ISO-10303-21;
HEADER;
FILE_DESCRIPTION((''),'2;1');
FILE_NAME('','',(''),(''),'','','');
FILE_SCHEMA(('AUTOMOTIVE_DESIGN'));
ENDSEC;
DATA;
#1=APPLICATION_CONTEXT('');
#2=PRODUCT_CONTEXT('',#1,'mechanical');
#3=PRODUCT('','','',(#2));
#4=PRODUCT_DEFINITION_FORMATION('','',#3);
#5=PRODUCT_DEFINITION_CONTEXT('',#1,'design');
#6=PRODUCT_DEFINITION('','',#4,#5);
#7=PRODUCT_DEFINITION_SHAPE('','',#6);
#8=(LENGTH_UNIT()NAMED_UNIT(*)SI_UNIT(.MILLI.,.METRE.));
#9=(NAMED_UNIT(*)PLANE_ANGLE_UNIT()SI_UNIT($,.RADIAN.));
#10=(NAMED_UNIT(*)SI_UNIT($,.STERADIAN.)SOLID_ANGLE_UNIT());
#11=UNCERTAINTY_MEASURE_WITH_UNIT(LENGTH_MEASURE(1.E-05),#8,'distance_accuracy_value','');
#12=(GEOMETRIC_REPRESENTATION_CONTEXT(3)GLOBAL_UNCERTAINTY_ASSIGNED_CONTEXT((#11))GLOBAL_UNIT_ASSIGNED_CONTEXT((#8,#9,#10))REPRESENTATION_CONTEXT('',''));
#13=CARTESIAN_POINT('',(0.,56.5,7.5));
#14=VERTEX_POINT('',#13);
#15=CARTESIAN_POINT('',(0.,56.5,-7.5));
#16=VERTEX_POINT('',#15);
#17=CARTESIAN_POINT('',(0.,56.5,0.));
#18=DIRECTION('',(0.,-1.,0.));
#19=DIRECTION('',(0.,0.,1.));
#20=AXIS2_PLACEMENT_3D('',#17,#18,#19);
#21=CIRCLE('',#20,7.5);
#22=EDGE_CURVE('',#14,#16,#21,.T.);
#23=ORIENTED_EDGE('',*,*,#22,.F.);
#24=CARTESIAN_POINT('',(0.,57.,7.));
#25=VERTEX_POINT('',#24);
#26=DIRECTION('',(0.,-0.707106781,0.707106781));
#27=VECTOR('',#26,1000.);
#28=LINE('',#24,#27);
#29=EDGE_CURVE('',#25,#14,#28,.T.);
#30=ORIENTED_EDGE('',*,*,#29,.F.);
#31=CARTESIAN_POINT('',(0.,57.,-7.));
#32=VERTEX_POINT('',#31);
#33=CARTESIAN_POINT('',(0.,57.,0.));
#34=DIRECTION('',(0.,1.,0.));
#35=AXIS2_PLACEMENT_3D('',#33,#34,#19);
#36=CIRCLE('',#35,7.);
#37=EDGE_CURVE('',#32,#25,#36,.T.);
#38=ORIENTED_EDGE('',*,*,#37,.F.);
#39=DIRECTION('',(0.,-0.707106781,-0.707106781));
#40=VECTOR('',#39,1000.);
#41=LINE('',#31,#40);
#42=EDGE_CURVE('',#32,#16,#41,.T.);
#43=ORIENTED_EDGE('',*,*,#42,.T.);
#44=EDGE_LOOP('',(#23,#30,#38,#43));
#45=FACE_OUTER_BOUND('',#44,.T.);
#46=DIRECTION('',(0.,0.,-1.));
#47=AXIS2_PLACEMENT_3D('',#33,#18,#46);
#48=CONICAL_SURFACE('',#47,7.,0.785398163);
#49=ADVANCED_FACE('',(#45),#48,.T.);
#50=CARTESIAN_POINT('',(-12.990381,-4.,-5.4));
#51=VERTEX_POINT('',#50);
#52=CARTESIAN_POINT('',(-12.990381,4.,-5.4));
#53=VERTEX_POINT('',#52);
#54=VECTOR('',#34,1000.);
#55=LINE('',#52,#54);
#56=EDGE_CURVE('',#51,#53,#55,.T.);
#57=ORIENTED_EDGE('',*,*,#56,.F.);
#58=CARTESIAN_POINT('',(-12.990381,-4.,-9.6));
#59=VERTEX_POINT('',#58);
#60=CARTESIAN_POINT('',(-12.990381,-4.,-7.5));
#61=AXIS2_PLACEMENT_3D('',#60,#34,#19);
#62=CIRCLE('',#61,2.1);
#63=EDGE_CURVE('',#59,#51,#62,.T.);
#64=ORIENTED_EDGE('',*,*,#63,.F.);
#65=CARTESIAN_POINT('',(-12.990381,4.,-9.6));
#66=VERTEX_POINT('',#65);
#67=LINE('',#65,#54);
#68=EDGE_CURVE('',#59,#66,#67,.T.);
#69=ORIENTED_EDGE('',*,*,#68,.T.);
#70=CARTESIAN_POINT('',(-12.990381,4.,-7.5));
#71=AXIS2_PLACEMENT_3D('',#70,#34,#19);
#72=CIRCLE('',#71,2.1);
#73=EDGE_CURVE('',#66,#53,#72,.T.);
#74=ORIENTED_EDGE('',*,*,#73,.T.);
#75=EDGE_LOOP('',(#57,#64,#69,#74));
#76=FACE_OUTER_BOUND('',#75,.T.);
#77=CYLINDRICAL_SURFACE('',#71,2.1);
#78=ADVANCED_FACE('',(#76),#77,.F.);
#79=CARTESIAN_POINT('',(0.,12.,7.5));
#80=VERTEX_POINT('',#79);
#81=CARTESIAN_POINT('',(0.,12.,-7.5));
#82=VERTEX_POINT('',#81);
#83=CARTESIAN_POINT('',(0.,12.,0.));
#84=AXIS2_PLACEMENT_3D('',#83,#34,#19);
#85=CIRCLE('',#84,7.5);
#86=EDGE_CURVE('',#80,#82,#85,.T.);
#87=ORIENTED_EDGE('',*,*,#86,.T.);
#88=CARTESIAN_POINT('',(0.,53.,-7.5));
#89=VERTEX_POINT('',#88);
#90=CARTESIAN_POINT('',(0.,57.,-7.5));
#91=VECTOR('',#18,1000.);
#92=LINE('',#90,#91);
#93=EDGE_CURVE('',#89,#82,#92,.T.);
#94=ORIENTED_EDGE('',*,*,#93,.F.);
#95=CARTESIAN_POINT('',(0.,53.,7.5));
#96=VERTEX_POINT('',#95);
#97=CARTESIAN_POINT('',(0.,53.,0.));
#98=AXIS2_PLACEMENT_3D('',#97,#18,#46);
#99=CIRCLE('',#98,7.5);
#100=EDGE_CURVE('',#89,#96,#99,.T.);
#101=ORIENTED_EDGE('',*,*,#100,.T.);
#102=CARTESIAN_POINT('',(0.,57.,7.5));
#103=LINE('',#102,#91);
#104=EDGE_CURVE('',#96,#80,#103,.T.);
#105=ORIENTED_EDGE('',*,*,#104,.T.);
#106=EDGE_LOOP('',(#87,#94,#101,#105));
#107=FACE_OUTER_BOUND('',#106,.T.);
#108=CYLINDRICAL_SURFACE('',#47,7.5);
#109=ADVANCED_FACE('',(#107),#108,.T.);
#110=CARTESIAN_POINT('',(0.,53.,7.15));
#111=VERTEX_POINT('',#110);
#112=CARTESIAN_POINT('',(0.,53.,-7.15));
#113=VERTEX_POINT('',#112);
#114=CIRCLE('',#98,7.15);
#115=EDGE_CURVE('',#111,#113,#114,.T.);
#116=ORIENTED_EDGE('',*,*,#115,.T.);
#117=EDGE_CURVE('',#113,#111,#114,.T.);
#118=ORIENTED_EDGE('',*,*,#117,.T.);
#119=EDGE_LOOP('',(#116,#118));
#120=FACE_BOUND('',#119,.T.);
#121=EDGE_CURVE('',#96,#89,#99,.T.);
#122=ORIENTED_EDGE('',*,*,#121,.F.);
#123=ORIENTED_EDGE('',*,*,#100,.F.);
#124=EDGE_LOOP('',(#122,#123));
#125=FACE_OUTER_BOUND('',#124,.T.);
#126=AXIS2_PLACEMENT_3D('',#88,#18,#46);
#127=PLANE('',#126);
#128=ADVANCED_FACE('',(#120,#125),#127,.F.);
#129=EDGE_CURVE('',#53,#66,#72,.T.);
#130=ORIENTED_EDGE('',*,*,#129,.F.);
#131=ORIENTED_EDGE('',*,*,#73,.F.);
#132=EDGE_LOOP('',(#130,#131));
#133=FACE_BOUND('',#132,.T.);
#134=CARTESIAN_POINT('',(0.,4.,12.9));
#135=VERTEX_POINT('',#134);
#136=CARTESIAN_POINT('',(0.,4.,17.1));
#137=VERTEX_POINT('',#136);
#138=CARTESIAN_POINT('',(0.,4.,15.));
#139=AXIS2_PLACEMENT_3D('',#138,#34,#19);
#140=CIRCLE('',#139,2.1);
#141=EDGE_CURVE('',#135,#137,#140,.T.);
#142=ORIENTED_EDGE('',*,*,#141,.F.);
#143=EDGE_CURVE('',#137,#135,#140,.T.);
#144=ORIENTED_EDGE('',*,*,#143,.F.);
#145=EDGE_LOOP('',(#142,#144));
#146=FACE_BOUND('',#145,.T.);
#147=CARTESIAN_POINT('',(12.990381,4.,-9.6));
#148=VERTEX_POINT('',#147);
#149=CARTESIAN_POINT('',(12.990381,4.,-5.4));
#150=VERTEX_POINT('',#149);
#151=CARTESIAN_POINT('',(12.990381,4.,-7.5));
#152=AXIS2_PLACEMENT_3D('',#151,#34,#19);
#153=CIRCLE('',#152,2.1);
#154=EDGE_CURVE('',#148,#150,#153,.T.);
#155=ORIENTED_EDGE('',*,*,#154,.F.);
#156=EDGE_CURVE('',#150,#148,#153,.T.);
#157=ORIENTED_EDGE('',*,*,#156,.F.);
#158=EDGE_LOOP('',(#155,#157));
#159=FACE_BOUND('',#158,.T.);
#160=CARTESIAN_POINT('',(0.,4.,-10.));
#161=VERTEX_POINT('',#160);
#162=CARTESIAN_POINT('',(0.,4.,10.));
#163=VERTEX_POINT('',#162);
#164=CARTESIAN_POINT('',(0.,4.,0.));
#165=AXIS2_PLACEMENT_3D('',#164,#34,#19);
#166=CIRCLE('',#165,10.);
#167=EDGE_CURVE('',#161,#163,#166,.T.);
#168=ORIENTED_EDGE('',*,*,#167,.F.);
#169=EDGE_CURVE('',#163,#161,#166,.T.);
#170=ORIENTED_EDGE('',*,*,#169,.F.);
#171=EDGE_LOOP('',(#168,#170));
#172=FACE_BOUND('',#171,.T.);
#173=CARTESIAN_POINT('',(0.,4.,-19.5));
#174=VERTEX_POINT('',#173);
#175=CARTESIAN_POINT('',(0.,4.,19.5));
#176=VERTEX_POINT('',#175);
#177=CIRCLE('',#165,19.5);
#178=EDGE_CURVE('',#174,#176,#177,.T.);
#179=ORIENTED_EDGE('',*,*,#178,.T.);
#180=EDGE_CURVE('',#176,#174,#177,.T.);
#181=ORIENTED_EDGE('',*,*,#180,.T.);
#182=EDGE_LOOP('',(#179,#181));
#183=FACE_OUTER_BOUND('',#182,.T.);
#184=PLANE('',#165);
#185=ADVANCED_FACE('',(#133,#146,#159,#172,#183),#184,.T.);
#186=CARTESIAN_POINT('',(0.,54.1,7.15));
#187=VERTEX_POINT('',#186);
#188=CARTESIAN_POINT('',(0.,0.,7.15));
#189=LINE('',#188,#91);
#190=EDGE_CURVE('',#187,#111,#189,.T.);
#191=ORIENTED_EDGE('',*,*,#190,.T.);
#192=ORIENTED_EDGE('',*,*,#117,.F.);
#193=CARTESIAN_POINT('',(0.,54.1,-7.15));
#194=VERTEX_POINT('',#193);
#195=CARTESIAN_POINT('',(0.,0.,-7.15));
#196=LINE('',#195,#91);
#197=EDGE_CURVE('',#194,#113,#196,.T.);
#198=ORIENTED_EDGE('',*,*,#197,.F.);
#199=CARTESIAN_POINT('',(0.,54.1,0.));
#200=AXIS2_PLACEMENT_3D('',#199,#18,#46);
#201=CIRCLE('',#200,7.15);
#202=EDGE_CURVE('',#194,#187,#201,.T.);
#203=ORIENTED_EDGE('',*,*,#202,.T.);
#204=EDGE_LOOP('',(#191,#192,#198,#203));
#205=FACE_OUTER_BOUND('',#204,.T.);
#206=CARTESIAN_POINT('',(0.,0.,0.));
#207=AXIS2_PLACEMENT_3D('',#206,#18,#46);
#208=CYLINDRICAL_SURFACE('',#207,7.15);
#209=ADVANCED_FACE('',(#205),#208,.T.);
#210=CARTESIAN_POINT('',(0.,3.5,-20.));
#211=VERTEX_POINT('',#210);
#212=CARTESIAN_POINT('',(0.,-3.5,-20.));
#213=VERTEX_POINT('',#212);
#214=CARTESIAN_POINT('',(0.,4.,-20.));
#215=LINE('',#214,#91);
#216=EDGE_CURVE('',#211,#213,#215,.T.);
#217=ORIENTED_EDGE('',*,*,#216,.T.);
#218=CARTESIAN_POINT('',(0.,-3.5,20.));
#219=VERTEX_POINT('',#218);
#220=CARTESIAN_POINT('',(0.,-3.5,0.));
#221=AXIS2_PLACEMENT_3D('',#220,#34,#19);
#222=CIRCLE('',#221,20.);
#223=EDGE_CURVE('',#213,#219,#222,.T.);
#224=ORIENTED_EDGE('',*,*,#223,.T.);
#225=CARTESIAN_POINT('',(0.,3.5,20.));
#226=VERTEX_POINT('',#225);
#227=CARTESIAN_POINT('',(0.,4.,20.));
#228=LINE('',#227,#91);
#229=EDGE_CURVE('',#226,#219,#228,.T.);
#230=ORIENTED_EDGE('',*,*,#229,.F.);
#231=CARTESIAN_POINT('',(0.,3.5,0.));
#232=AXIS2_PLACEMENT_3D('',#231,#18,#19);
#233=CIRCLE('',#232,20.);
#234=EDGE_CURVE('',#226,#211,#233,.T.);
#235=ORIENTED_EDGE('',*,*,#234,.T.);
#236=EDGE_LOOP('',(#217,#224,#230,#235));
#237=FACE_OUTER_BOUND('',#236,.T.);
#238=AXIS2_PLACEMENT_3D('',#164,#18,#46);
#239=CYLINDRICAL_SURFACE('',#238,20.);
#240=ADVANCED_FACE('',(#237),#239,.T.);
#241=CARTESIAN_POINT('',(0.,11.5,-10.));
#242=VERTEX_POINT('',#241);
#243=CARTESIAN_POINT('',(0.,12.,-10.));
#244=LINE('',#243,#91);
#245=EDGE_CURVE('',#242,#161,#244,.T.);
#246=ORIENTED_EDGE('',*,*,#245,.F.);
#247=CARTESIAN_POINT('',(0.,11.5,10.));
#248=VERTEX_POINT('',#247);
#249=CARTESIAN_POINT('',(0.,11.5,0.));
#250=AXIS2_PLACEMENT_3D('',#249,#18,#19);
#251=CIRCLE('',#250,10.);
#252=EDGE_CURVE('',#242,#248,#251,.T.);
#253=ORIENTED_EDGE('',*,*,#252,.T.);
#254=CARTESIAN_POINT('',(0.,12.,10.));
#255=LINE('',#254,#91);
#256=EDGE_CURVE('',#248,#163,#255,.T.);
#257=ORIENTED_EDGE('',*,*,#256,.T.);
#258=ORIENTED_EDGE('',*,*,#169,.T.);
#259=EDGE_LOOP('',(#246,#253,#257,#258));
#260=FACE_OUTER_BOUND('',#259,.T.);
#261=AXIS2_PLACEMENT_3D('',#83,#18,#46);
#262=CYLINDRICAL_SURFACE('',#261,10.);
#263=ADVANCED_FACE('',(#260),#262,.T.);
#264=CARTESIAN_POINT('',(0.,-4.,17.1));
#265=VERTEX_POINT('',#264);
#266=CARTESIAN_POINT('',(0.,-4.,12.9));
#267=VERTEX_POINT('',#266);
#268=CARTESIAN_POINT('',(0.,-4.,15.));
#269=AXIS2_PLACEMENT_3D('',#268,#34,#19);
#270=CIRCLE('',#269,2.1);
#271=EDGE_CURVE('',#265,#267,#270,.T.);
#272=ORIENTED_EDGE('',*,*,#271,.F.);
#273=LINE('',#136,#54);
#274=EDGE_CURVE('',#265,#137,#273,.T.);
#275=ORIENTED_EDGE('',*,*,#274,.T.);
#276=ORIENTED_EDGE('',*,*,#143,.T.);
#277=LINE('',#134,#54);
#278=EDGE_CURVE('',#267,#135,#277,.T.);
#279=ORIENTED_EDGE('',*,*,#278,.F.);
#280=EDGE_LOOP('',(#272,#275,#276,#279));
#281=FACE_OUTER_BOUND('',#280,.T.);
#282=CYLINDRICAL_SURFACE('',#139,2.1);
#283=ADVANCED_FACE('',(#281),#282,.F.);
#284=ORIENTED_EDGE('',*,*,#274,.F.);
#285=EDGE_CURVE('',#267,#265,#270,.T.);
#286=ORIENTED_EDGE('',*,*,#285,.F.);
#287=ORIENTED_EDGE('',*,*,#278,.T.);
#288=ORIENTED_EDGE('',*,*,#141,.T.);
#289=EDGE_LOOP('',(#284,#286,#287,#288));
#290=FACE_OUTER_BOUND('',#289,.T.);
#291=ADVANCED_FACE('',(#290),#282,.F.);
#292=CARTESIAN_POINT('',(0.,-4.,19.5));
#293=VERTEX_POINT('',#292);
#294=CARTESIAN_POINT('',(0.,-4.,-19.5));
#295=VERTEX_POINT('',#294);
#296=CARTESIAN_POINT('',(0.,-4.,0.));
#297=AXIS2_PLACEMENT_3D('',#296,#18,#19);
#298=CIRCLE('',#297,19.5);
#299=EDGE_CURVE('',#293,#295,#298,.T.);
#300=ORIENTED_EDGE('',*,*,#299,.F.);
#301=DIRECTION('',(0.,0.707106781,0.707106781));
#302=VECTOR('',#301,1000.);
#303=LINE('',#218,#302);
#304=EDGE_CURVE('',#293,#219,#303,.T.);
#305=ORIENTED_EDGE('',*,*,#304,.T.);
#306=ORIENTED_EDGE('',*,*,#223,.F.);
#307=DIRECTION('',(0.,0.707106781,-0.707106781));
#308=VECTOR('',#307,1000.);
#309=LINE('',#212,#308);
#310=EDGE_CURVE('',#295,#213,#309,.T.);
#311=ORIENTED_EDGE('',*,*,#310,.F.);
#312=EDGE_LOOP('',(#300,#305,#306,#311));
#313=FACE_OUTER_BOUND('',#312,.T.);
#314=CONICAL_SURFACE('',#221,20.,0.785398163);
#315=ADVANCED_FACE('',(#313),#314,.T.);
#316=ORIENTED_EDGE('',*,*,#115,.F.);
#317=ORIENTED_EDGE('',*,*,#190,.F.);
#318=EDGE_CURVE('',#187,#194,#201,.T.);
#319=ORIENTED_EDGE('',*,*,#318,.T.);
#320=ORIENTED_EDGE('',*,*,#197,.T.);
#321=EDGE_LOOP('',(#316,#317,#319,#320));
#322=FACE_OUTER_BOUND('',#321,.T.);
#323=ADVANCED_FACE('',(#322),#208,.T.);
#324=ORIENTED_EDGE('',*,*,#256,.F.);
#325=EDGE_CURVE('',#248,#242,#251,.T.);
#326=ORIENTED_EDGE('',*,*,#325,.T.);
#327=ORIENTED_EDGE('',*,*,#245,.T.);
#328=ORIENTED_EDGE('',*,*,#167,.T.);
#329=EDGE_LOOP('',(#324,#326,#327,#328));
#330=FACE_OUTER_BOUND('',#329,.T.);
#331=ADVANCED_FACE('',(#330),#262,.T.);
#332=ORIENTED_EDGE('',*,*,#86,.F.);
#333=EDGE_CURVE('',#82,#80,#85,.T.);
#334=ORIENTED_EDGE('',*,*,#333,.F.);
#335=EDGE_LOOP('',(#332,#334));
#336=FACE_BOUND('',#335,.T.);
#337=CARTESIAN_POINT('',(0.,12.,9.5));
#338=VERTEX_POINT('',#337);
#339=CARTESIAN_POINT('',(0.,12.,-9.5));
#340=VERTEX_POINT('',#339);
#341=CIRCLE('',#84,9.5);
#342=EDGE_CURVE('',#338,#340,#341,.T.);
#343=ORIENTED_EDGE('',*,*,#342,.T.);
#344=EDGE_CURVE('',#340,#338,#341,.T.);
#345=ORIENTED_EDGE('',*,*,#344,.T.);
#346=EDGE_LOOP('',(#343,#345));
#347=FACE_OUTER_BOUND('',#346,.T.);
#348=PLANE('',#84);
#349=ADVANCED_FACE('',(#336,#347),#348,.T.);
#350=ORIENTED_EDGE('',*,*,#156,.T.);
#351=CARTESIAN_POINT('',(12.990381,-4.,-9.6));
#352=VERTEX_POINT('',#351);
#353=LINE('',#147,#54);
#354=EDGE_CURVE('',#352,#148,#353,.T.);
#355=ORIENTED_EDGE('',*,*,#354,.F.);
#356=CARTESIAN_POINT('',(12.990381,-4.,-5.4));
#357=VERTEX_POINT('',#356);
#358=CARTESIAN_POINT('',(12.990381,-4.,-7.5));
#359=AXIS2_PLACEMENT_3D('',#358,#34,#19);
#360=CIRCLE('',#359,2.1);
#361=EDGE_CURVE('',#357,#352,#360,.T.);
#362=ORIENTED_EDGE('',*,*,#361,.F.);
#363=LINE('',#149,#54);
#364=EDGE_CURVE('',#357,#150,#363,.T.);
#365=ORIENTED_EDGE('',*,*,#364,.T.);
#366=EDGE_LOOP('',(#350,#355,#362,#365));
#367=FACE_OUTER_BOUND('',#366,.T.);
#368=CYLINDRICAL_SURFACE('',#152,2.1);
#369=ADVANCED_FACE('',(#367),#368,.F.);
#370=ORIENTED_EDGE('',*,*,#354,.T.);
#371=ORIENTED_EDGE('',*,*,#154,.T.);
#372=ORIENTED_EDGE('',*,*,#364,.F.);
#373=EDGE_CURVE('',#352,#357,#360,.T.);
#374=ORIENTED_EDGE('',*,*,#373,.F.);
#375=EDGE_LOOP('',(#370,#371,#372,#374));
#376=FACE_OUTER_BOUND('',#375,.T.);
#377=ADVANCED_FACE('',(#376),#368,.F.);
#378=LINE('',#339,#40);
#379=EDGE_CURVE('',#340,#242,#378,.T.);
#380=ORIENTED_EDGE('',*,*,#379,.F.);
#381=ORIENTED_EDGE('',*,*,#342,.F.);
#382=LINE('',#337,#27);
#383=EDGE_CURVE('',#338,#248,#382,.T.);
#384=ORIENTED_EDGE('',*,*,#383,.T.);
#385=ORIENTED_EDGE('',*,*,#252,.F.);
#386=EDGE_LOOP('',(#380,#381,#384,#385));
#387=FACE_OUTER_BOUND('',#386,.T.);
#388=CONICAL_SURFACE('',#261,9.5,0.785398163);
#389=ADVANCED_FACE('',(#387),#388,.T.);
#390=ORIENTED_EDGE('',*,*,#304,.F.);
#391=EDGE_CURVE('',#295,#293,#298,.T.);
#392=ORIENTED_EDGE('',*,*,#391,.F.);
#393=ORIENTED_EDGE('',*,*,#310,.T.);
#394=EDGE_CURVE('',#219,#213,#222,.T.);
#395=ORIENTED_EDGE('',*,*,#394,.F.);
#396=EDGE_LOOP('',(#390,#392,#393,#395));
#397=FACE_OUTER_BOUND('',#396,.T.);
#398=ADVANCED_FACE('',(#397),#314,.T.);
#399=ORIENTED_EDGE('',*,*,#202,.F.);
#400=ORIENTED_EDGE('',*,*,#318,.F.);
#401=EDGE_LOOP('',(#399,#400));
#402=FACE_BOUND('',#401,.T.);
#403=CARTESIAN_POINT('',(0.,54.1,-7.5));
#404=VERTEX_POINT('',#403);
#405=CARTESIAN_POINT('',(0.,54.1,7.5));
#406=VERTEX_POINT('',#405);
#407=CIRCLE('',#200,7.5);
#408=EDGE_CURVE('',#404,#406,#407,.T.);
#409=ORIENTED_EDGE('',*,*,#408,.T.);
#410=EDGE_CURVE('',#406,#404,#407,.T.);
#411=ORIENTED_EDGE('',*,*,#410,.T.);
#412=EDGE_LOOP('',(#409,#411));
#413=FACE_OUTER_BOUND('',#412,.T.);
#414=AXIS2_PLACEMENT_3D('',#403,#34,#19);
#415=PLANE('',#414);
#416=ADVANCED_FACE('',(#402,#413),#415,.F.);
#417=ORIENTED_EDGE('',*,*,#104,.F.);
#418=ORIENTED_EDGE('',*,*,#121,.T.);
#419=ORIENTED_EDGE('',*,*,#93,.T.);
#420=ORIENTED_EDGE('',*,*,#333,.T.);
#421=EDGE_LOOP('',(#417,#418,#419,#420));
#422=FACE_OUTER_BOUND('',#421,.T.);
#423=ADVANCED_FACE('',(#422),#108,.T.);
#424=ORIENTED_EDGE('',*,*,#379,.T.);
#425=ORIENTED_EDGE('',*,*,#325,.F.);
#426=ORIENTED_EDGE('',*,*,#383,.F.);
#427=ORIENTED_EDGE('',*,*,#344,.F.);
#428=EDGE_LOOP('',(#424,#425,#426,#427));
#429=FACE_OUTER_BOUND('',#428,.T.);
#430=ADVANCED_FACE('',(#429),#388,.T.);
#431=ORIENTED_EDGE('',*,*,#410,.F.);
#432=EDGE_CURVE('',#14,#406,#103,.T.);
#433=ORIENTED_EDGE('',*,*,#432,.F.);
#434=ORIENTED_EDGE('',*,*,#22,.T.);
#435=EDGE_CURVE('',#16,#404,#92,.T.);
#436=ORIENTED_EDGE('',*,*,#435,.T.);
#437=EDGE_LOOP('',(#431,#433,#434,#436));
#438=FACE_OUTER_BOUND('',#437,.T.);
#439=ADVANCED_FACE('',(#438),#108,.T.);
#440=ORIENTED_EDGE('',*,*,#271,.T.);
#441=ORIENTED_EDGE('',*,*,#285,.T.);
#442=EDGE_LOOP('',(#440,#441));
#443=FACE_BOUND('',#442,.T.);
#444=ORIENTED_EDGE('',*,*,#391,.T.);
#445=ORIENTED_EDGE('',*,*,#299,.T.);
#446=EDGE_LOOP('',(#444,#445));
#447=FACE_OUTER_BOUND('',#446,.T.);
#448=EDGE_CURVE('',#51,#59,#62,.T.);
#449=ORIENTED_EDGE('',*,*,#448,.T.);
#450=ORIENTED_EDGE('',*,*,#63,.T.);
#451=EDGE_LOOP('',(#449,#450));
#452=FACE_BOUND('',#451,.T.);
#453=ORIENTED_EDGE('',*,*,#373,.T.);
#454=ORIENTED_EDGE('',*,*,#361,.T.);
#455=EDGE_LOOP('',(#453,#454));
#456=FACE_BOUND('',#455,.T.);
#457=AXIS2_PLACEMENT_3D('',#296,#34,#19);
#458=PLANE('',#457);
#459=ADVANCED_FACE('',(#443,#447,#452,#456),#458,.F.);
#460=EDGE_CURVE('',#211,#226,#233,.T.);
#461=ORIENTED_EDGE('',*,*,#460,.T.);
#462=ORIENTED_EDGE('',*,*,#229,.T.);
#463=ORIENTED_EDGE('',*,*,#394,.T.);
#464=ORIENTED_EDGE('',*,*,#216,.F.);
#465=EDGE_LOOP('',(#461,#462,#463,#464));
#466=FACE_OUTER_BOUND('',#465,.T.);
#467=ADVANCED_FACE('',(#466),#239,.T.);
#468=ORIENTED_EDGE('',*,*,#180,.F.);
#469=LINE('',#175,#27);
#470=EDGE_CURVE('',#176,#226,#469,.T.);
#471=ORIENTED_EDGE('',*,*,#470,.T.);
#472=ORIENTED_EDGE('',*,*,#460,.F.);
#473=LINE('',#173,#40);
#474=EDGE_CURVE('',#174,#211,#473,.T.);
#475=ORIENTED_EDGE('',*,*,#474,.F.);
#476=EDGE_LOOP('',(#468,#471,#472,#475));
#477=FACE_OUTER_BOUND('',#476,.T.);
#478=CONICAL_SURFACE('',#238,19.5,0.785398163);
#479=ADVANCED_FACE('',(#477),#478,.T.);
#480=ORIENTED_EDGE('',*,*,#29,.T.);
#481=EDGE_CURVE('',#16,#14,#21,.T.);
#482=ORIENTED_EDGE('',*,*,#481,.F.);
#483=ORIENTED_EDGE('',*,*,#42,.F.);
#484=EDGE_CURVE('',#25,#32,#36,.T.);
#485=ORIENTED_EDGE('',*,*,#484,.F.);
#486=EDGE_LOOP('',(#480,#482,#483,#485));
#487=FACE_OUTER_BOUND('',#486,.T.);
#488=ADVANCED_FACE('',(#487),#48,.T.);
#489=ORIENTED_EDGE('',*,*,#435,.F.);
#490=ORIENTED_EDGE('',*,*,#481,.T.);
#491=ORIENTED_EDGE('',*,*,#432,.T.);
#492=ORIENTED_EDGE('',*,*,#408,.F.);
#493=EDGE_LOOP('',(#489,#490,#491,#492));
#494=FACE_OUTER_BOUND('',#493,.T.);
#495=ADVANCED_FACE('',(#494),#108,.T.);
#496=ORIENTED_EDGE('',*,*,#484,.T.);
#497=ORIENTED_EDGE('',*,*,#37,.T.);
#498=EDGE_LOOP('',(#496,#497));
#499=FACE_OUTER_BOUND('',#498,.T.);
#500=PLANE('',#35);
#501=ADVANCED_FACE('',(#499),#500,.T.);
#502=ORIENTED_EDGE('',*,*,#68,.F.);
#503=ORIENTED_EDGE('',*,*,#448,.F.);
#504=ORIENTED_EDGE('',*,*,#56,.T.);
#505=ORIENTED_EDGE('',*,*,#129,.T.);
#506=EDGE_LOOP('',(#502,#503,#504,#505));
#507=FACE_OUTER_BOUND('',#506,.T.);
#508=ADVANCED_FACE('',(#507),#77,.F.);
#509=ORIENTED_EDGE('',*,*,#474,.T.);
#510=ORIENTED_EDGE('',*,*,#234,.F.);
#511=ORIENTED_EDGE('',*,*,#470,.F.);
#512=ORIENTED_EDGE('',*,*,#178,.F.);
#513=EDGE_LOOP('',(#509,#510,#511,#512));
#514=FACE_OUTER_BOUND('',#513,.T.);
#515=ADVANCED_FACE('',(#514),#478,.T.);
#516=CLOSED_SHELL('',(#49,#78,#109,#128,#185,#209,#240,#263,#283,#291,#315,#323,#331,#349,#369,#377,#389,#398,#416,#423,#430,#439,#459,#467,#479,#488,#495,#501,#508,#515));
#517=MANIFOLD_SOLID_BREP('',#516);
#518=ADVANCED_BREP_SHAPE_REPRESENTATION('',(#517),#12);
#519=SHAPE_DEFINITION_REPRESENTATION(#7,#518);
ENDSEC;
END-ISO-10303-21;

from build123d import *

# Parameters (mm, degrees)
SKETCH_1_R         = 20
EXTRUDE_1_DEPTH    = 4
SKETCH_2_R         = 10
EXTRUDE_2_DEPTH    = 8
SKETCH_3_R         = 7.5
EXTRUDE_3_DEPTH    = 45
SKETCH_4_W         = 0.35
SKETCH_4_H         = 1.1
HOLE_WIZARD_M5_1_D = 4.2
CHAMFER_1_SIZE     = 0.5
CHAMFER_2_SIZE     = 0.5


with BuildPart() as part:
    # 草图1 → 凸台-拉伸1 (new, symmetric)
    with BuildSketch(Plane(origin=(0, 0, 0), x_dir=(1, 0, 0), z_dir=(0, 1, 0))):
        with Locations(Location((0, 0, 0), (0, 0, 270))):
            Circle(SKETCH_1_R)
    extrude(amount=EXTRUDE_1_DEPTH, both=True)

    # 草图2 → 凸台-拉伸2 (add)
    with BuildSketch(Plane(origin=(0, 4, 0), x_dir=(1, 0, 0), z_dir=(0, 1, 0))):
        with Locations(Location((0, 0, 0), (0, 0, 270))):
            Circle(SKETCH_2_R)
    extrude(amount=EXTRUDE_2_DEPTH)

    # 草图3 → 凸台-拉伸3 (add)
    with BuildSketch(Plane(origin=(0, 12, 0), x_dir=(1, 0, 0), z_dir=(0, 1, 0))):
        with Locations(Location((0, 0, 0), (0, 0, 90))):
            Circle(SKETCH_3_R)
    extrude(amount=EXTRUDE_3_DEPTH)

    # 草图4 → 切除-旋转1 (revolve, cut)
    with BuildSketch(Plane(origin=(0, 0, 0), x_dir=(0, 0, -1), z_dir=(1, 0, 0))):
        with Locations((7.325, 53.55)):
            Rectangle(SKETCH_4_W, SKETCH_4_H)
    revolve(axis=Axis((0, 0, 0), (0, 1, 0)), mode=Mode.SUBTRACT)

    # M5 螺纹孔1 (through all)
    with Locations(Plane(origin=(0, 4, 0), x_dir=(1, 0, 0), z_dir=(0, 1, 0))):
        with Locations((-12.990381057, 7.5), (12.990381057, 7.5), (0, -15)):
            Hole(HOLE_WIZARD_M5_1_D / 2)

    # 倒角1
    chamfer_1_edges = [part.edges().sort_by_distance(p)[0] for p in [
        (0, 57, 7.5),
        (0, 12, -10),
    ]]
    chamfer(chamfer_1_edges, length=CHAMFER_1_SIZE)

    # 倒角2
    chamfer_2_edges = [part.edges().sort_by_distance(p)[0] for p in [
        (0, -4, -20),
        (0, 4, -20),
    ]]
    chamfer(chamfer_2_edges, length=CHAMFER_2_SIZE)


solid = part.part
